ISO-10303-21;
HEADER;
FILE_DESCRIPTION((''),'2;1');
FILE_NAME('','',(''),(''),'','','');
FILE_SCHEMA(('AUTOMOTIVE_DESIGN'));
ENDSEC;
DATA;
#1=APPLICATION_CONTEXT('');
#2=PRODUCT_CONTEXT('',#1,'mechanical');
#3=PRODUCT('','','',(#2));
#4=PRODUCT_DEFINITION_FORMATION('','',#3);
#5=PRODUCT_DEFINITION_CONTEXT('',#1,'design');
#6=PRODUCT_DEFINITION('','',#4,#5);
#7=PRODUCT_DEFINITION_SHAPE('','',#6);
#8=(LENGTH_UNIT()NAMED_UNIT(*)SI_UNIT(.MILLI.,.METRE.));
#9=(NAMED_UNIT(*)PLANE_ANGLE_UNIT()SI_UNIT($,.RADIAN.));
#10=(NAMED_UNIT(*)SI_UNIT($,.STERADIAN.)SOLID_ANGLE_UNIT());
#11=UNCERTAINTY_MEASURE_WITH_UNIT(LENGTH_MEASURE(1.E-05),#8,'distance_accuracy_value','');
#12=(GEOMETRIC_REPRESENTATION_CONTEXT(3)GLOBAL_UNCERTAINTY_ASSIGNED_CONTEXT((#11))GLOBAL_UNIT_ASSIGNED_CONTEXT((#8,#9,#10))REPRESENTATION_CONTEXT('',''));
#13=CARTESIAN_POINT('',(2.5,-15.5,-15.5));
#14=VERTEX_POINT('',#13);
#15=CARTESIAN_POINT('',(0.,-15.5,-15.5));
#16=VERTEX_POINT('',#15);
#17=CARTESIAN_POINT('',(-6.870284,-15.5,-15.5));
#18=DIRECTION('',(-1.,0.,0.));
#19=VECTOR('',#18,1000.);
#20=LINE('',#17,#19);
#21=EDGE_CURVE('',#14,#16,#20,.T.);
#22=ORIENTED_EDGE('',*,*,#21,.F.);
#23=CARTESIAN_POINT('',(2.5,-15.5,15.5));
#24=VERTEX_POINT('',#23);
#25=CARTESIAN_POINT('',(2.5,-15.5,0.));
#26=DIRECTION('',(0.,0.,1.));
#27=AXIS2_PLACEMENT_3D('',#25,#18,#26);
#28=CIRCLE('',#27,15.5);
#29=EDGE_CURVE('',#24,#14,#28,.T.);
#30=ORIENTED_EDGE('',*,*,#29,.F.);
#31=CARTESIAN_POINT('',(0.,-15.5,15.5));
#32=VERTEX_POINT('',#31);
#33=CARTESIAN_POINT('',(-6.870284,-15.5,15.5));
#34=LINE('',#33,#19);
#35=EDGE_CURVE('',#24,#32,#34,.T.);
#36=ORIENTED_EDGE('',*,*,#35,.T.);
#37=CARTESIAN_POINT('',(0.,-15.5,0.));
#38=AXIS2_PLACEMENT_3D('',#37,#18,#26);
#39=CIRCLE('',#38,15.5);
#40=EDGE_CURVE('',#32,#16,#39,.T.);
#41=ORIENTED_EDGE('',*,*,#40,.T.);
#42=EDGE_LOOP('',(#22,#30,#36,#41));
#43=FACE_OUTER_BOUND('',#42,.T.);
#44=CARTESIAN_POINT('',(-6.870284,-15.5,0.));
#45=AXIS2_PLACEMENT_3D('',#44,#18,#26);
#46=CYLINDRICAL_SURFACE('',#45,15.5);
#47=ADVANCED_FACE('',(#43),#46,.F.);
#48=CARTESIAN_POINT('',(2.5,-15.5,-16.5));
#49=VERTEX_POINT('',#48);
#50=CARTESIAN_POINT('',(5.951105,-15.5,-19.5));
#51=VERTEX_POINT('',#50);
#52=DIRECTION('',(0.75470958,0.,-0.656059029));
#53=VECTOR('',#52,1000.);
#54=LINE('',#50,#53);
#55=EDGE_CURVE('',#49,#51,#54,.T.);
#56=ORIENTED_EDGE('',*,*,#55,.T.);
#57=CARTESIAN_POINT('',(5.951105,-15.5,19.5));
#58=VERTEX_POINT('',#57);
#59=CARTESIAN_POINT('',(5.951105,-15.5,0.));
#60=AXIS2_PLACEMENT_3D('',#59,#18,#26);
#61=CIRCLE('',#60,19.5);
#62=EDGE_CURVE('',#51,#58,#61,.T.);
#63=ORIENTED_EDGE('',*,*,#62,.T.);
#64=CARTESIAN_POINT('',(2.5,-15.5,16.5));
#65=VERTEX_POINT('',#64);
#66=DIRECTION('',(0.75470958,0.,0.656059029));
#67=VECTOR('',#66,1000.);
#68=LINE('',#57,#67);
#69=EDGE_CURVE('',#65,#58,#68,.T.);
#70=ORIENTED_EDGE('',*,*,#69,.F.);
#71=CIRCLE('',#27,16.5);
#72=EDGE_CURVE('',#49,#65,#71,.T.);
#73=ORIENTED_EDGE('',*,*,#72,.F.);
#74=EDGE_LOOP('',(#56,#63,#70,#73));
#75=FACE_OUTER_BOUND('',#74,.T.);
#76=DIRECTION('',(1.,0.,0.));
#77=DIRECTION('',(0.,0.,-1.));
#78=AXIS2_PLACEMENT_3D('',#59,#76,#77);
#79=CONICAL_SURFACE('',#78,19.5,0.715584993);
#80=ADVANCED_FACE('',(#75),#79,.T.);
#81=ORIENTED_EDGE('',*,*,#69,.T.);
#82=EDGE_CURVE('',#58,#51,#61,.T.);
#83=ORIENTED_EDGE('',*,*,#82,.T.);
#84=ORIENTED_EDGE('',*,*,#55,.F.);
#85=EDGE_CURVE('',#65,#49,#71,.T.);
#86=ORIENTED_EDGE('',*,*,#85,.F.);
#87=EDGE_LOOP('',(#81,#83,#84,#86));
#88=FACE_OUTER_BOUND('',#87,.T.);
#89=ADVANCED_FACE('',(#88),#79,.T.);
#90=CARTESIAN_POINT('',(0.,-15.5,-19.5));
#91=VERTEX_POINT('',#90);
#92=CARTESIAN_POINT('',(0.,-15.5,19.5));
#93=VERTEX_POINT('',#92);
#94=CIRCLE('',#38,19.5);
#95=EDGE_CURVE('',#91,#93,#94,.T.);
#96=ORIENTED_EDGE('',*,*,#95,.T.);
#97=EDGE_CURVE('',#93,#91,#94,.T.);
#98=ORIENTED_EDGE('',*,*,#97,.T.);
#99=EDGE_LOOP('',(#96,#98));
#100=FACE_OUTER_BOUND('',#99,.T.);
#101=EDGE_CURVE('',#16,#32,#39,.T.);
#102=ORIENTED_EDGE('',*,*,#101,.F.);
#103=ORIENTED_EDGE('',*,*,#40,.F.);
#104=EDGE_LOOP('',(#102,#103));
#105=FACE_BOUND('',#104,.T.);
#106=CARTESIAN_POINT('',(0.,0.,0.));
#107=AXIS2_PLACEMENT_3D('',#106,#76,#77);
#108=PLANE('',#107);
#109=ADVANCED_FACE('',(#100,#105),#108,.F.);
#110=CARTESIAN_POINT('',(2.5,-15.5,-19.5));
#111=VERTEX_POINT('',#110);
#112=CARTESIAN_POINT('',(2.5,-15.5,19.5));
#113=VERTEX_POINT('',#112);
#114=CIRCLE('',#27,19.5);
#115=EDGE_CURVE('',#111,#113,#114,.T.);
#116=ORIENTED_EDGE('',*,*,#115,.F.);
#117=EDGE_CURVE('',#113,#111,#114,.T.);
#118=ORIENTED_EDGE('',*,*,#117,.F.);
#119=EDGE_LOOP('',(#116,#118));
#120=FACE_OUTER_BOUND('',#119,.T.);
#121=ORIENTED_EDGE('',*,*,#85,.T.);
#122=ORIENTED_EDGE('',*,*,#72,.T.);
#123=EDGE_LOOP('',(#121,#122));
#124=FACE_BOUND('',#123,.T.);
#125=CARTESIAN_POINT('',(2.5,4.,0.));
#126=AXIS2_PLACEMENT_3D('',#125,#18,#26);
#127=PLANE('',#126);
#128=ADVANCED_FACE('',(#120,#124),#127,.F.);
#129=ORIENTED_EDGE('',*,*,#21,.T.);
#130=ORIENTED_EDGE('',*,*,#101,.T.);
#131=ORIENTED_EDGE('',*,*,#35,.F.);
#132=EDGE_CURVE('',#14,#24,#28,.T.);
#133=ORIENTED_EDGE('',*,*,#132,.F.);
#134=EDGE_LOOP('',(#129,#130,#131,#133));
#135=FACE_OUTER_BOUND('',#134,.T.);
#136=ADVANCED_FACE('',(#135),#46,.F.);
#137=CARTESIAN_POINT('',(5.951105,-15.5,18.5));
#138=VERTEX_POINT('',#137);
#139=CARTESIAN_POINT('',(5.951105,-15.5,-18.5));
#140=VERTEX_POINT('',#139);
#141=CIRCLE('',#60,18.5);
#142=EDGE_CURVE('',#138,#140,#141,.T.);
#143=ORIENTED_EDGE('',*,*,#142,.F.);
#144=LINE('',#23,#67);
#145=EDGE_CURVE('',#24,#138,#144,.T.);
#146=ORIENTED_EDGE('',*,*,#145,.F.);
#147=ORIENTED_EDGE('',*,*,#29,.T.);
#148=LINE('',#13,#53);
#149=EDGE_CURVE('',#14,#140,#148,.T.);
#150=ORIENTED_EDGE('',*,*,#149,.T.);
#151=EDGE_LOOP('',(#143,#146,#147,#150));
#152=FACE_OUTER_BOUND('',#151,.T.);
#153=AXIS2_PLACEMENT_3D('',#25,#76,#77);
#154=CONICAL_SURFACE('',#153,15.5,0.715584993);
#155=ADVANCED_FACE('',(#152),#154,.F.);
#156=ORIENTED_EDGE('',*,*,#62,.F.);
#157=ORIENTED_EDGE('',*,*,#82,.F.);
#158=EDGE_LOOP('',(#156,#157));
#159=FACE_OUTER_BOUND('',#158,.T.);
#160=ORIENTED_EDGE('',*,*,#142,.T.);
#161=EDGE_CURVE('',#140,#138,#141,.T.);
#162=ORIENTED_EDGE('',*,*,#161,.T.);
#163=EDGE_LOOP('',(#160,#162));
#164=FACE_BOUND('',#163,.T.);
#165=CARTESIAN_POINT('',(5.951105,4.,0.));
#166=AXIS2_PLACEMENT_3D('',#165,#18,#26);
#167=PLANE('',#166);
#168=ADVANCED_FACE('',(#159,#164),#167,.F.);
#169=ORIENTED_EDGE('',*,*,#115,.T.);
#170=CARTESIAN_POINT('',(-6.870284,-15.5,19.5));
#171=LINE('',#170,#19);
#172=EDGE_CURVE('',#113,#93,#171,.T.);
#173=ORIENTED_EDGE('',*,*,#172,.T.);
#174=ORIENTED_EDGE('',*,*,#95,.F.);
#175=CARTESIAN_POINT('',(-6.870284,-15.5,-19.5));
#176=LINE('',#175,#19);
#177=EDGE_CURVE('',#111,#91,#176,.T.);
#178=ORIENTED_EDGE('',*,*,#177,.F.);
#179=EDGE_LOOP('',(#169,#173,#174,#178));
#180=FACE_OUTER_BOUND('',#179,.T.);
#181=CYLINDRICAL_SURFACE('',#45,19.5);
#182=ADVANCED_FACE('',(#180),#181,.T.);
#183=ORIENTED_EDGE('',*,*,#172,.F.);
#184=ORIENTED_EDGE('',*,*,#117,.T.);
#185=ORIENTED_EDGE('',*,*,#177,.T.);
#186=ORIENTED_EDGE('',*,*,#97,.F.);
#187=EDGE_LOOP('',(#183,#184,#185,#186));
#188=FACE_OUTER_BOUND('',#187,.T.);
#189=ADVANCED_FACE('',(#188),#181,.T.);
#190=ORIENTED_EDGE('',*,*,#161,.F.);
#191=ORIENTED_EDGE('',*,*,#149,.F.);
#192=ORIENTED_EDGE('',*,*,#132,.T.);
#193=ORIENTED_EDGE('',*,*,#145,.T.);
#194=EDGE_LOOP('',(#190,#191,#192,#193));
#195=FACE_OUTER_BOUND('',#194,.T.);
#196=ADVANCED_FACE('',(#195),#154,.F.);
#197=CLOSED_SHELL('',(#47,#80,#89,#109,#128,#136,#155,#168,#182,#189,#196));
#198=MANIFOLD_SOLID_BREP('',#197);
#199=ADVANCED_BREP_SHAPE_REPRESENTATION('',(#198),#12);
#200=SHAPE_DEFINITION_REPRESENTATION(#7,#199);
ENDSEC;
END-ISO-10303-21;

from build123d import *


with BuildPart() as part:
    # 草图1 → 旋转1 (revolve)
    with BuildSketch(Plane.XY, mode=Mode.PRIVATE) as revolve_1_sk:
        Polygon((0, 0), (2.5, 0), (5.951105222, 3), (5.951105222, 4), (2.5, 1), (2.5, 4), (0, 4), align=None)
    revolve(revolve_1_sk.sketch.rotate(Axis((-6.870284449, -15.5, 0), (1, 0, 0)), 90), axis=Axis((-6.870284449, -15.5, 0), (1, 0, 0)))


solid = part.part
